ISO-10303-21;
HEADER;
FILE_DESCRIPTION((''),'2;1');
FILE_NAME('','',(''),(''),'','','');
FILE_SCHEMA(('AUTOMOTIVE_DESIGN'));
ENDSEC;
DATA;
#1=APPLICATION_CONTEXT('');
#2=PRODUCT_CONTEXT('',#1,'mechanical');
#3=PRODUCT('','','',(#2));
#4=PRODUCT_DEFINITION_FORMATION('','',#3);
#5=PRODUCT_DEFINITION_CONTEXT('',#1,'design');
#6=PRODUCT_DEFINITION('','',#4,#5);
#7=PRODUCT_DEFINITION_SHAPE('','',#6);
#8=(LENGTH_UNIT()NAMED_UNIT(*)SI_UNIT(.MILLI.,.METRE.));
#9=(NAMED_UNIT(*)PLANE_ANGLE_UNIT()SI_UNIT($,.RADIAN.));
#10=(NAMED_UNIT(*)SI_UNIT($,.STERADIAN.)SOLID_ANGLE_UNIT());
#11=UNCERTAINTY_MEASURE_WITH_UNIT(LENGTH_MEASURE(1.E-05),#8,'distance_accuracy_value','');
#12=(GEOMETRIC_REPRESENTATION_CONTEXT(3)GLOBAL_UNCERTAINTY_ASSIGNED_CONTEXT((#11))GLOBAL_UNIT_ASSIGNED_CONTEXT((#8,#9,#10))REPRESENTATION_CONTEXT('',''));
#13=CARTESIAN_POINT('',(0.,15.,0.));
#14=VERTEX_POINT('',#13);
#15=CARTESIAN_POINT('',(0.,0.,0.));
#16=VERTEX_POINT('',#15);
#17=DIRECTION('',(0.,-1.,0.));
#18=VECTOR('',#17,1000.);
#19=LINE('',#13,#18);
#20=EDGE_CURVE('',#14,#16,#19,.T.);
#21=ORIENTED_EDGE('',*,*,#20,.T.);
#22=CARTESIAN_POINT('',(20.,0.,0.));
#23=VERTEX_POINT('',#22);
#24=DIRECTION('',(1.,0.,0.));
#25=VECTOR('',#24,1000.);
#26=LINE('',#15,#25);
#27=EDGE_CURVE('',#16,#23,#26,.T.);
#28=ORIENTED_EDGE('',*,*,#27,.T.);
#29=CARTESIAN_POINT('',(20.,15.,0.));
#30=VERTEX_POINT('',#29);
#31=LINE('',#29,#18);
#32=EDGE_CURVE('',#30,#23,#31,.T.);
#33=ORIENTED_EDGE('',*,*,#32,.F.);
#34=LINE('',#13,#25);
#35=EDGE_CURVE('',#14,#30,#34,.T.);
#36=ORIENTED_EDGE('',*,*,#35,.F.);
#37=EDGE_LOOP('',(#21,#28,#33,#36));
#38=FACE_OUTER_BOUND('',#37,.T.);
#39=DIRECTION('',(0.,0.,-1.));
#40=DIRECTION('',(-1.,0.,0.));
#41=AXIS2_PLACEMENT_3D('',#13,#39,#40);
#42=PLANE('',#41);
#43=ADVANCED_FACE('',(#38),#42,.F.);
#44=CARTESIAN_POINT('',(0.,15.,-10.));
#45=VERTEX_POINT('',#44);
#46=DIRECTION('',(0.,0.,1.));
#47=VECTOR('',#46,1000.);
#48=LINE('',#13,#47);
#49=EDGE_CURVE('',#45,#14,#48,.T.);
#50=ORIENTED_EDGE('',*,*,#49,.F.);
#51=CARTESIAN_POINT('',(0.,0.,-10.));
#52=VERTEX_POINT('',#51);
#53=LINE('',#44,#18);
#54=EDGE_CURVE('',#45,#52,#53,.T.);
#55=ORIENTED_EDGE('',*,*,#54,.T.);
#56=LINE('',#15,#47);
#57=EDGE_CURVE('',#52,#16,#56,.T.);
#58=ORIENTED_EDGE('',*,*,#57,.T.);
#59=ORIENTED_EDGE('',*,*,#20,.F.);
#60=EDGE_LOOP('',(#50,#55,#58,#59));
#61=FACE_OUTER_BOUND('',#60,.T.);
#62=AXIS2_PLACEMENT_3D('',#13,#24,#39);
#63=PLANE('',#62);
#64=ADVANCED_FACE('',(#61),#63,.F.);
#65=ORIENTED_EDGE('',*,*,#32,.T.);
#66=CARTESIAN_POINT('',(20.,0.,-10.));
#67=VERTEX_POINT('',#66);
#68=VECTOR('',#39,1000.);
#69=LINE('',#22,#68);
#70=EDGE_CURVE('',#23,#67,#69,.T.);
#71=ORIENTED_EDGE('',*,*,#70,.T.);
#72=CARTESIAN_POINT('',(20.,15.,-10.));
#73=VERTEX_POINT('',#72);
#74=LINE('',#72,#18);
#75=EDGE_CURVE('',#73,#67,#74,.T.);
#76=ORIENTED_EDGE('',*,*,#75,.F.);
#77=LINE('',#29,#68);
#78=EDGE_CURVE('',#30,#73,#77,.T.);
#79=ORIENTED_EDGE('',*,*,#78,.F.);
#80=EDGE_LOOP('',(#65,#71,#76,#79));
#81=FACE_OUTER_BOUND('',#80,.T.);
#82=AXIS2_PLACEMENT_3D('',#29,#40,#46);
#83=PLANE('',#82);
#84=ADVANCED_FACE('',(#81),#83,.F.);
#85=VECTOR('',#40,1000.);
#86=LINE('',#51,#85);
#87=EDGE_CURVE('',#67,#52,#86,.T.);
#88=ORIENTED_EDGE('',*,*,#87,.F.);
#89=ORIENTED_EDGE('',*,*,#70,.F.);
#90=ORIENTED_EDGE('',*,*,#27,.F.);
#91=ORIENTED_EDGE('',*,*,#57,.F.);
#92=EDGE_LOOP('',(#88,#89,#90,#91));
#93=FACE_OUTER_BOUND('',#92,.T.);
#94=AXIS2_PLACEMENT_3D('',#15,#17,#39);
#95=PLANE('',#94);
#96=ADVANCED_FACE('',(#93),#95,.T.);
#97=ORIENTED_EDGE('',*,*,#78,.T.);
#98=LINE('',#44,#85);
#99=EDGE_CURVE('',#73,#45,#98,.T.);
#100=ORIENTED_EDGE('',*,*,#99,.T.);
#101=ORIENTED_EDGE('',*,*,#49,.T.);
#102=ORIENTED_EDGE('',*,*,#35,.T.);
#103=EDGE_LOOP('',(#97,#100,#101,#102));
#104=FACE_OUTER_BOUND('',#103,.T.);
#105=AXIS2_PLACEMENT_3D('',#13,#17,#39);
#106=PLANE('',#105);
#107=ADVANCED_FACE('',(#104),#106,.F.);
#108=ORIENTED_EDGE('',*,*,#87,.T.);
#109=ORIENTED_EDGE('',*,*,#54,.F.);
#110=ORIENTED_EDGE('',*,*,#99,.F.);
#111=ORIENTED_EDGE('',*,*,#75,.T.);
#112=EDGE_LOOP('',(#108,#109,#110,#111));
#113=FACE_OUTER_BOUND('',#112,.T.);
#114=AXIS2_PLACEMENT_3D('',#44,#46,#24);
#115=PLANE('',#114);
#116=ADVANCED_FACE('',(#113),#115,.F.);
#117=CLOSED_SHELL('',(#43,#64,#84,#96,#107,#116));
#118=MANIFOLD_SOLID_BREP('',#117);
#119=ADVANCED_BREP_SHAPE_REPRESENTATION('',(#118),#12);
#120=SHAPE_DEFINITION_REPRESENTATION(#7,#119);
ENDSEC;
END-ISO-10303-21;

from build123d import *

# Parameters (mm, degrees)
SKETCH1_W           = 20
SKETCH1_H           = 10
BOSS_EXTRUDE1_DEPTH = 15


with BuildPart() as part:
    # Sketch1 → Boss-Extrude1 (new body)
    with BuildSketch(Plane(origin=(0, 0, 0), x_dir=(1, 0, 0), z_dir=(0, 1, 0))):
        with Locations((10, 5)):
            Rectangle(SKETCH1_W, SKETCH1_H)
    extrude(amount=BOSS_EXTRUDE1_DEPTH)


solid = part.part
